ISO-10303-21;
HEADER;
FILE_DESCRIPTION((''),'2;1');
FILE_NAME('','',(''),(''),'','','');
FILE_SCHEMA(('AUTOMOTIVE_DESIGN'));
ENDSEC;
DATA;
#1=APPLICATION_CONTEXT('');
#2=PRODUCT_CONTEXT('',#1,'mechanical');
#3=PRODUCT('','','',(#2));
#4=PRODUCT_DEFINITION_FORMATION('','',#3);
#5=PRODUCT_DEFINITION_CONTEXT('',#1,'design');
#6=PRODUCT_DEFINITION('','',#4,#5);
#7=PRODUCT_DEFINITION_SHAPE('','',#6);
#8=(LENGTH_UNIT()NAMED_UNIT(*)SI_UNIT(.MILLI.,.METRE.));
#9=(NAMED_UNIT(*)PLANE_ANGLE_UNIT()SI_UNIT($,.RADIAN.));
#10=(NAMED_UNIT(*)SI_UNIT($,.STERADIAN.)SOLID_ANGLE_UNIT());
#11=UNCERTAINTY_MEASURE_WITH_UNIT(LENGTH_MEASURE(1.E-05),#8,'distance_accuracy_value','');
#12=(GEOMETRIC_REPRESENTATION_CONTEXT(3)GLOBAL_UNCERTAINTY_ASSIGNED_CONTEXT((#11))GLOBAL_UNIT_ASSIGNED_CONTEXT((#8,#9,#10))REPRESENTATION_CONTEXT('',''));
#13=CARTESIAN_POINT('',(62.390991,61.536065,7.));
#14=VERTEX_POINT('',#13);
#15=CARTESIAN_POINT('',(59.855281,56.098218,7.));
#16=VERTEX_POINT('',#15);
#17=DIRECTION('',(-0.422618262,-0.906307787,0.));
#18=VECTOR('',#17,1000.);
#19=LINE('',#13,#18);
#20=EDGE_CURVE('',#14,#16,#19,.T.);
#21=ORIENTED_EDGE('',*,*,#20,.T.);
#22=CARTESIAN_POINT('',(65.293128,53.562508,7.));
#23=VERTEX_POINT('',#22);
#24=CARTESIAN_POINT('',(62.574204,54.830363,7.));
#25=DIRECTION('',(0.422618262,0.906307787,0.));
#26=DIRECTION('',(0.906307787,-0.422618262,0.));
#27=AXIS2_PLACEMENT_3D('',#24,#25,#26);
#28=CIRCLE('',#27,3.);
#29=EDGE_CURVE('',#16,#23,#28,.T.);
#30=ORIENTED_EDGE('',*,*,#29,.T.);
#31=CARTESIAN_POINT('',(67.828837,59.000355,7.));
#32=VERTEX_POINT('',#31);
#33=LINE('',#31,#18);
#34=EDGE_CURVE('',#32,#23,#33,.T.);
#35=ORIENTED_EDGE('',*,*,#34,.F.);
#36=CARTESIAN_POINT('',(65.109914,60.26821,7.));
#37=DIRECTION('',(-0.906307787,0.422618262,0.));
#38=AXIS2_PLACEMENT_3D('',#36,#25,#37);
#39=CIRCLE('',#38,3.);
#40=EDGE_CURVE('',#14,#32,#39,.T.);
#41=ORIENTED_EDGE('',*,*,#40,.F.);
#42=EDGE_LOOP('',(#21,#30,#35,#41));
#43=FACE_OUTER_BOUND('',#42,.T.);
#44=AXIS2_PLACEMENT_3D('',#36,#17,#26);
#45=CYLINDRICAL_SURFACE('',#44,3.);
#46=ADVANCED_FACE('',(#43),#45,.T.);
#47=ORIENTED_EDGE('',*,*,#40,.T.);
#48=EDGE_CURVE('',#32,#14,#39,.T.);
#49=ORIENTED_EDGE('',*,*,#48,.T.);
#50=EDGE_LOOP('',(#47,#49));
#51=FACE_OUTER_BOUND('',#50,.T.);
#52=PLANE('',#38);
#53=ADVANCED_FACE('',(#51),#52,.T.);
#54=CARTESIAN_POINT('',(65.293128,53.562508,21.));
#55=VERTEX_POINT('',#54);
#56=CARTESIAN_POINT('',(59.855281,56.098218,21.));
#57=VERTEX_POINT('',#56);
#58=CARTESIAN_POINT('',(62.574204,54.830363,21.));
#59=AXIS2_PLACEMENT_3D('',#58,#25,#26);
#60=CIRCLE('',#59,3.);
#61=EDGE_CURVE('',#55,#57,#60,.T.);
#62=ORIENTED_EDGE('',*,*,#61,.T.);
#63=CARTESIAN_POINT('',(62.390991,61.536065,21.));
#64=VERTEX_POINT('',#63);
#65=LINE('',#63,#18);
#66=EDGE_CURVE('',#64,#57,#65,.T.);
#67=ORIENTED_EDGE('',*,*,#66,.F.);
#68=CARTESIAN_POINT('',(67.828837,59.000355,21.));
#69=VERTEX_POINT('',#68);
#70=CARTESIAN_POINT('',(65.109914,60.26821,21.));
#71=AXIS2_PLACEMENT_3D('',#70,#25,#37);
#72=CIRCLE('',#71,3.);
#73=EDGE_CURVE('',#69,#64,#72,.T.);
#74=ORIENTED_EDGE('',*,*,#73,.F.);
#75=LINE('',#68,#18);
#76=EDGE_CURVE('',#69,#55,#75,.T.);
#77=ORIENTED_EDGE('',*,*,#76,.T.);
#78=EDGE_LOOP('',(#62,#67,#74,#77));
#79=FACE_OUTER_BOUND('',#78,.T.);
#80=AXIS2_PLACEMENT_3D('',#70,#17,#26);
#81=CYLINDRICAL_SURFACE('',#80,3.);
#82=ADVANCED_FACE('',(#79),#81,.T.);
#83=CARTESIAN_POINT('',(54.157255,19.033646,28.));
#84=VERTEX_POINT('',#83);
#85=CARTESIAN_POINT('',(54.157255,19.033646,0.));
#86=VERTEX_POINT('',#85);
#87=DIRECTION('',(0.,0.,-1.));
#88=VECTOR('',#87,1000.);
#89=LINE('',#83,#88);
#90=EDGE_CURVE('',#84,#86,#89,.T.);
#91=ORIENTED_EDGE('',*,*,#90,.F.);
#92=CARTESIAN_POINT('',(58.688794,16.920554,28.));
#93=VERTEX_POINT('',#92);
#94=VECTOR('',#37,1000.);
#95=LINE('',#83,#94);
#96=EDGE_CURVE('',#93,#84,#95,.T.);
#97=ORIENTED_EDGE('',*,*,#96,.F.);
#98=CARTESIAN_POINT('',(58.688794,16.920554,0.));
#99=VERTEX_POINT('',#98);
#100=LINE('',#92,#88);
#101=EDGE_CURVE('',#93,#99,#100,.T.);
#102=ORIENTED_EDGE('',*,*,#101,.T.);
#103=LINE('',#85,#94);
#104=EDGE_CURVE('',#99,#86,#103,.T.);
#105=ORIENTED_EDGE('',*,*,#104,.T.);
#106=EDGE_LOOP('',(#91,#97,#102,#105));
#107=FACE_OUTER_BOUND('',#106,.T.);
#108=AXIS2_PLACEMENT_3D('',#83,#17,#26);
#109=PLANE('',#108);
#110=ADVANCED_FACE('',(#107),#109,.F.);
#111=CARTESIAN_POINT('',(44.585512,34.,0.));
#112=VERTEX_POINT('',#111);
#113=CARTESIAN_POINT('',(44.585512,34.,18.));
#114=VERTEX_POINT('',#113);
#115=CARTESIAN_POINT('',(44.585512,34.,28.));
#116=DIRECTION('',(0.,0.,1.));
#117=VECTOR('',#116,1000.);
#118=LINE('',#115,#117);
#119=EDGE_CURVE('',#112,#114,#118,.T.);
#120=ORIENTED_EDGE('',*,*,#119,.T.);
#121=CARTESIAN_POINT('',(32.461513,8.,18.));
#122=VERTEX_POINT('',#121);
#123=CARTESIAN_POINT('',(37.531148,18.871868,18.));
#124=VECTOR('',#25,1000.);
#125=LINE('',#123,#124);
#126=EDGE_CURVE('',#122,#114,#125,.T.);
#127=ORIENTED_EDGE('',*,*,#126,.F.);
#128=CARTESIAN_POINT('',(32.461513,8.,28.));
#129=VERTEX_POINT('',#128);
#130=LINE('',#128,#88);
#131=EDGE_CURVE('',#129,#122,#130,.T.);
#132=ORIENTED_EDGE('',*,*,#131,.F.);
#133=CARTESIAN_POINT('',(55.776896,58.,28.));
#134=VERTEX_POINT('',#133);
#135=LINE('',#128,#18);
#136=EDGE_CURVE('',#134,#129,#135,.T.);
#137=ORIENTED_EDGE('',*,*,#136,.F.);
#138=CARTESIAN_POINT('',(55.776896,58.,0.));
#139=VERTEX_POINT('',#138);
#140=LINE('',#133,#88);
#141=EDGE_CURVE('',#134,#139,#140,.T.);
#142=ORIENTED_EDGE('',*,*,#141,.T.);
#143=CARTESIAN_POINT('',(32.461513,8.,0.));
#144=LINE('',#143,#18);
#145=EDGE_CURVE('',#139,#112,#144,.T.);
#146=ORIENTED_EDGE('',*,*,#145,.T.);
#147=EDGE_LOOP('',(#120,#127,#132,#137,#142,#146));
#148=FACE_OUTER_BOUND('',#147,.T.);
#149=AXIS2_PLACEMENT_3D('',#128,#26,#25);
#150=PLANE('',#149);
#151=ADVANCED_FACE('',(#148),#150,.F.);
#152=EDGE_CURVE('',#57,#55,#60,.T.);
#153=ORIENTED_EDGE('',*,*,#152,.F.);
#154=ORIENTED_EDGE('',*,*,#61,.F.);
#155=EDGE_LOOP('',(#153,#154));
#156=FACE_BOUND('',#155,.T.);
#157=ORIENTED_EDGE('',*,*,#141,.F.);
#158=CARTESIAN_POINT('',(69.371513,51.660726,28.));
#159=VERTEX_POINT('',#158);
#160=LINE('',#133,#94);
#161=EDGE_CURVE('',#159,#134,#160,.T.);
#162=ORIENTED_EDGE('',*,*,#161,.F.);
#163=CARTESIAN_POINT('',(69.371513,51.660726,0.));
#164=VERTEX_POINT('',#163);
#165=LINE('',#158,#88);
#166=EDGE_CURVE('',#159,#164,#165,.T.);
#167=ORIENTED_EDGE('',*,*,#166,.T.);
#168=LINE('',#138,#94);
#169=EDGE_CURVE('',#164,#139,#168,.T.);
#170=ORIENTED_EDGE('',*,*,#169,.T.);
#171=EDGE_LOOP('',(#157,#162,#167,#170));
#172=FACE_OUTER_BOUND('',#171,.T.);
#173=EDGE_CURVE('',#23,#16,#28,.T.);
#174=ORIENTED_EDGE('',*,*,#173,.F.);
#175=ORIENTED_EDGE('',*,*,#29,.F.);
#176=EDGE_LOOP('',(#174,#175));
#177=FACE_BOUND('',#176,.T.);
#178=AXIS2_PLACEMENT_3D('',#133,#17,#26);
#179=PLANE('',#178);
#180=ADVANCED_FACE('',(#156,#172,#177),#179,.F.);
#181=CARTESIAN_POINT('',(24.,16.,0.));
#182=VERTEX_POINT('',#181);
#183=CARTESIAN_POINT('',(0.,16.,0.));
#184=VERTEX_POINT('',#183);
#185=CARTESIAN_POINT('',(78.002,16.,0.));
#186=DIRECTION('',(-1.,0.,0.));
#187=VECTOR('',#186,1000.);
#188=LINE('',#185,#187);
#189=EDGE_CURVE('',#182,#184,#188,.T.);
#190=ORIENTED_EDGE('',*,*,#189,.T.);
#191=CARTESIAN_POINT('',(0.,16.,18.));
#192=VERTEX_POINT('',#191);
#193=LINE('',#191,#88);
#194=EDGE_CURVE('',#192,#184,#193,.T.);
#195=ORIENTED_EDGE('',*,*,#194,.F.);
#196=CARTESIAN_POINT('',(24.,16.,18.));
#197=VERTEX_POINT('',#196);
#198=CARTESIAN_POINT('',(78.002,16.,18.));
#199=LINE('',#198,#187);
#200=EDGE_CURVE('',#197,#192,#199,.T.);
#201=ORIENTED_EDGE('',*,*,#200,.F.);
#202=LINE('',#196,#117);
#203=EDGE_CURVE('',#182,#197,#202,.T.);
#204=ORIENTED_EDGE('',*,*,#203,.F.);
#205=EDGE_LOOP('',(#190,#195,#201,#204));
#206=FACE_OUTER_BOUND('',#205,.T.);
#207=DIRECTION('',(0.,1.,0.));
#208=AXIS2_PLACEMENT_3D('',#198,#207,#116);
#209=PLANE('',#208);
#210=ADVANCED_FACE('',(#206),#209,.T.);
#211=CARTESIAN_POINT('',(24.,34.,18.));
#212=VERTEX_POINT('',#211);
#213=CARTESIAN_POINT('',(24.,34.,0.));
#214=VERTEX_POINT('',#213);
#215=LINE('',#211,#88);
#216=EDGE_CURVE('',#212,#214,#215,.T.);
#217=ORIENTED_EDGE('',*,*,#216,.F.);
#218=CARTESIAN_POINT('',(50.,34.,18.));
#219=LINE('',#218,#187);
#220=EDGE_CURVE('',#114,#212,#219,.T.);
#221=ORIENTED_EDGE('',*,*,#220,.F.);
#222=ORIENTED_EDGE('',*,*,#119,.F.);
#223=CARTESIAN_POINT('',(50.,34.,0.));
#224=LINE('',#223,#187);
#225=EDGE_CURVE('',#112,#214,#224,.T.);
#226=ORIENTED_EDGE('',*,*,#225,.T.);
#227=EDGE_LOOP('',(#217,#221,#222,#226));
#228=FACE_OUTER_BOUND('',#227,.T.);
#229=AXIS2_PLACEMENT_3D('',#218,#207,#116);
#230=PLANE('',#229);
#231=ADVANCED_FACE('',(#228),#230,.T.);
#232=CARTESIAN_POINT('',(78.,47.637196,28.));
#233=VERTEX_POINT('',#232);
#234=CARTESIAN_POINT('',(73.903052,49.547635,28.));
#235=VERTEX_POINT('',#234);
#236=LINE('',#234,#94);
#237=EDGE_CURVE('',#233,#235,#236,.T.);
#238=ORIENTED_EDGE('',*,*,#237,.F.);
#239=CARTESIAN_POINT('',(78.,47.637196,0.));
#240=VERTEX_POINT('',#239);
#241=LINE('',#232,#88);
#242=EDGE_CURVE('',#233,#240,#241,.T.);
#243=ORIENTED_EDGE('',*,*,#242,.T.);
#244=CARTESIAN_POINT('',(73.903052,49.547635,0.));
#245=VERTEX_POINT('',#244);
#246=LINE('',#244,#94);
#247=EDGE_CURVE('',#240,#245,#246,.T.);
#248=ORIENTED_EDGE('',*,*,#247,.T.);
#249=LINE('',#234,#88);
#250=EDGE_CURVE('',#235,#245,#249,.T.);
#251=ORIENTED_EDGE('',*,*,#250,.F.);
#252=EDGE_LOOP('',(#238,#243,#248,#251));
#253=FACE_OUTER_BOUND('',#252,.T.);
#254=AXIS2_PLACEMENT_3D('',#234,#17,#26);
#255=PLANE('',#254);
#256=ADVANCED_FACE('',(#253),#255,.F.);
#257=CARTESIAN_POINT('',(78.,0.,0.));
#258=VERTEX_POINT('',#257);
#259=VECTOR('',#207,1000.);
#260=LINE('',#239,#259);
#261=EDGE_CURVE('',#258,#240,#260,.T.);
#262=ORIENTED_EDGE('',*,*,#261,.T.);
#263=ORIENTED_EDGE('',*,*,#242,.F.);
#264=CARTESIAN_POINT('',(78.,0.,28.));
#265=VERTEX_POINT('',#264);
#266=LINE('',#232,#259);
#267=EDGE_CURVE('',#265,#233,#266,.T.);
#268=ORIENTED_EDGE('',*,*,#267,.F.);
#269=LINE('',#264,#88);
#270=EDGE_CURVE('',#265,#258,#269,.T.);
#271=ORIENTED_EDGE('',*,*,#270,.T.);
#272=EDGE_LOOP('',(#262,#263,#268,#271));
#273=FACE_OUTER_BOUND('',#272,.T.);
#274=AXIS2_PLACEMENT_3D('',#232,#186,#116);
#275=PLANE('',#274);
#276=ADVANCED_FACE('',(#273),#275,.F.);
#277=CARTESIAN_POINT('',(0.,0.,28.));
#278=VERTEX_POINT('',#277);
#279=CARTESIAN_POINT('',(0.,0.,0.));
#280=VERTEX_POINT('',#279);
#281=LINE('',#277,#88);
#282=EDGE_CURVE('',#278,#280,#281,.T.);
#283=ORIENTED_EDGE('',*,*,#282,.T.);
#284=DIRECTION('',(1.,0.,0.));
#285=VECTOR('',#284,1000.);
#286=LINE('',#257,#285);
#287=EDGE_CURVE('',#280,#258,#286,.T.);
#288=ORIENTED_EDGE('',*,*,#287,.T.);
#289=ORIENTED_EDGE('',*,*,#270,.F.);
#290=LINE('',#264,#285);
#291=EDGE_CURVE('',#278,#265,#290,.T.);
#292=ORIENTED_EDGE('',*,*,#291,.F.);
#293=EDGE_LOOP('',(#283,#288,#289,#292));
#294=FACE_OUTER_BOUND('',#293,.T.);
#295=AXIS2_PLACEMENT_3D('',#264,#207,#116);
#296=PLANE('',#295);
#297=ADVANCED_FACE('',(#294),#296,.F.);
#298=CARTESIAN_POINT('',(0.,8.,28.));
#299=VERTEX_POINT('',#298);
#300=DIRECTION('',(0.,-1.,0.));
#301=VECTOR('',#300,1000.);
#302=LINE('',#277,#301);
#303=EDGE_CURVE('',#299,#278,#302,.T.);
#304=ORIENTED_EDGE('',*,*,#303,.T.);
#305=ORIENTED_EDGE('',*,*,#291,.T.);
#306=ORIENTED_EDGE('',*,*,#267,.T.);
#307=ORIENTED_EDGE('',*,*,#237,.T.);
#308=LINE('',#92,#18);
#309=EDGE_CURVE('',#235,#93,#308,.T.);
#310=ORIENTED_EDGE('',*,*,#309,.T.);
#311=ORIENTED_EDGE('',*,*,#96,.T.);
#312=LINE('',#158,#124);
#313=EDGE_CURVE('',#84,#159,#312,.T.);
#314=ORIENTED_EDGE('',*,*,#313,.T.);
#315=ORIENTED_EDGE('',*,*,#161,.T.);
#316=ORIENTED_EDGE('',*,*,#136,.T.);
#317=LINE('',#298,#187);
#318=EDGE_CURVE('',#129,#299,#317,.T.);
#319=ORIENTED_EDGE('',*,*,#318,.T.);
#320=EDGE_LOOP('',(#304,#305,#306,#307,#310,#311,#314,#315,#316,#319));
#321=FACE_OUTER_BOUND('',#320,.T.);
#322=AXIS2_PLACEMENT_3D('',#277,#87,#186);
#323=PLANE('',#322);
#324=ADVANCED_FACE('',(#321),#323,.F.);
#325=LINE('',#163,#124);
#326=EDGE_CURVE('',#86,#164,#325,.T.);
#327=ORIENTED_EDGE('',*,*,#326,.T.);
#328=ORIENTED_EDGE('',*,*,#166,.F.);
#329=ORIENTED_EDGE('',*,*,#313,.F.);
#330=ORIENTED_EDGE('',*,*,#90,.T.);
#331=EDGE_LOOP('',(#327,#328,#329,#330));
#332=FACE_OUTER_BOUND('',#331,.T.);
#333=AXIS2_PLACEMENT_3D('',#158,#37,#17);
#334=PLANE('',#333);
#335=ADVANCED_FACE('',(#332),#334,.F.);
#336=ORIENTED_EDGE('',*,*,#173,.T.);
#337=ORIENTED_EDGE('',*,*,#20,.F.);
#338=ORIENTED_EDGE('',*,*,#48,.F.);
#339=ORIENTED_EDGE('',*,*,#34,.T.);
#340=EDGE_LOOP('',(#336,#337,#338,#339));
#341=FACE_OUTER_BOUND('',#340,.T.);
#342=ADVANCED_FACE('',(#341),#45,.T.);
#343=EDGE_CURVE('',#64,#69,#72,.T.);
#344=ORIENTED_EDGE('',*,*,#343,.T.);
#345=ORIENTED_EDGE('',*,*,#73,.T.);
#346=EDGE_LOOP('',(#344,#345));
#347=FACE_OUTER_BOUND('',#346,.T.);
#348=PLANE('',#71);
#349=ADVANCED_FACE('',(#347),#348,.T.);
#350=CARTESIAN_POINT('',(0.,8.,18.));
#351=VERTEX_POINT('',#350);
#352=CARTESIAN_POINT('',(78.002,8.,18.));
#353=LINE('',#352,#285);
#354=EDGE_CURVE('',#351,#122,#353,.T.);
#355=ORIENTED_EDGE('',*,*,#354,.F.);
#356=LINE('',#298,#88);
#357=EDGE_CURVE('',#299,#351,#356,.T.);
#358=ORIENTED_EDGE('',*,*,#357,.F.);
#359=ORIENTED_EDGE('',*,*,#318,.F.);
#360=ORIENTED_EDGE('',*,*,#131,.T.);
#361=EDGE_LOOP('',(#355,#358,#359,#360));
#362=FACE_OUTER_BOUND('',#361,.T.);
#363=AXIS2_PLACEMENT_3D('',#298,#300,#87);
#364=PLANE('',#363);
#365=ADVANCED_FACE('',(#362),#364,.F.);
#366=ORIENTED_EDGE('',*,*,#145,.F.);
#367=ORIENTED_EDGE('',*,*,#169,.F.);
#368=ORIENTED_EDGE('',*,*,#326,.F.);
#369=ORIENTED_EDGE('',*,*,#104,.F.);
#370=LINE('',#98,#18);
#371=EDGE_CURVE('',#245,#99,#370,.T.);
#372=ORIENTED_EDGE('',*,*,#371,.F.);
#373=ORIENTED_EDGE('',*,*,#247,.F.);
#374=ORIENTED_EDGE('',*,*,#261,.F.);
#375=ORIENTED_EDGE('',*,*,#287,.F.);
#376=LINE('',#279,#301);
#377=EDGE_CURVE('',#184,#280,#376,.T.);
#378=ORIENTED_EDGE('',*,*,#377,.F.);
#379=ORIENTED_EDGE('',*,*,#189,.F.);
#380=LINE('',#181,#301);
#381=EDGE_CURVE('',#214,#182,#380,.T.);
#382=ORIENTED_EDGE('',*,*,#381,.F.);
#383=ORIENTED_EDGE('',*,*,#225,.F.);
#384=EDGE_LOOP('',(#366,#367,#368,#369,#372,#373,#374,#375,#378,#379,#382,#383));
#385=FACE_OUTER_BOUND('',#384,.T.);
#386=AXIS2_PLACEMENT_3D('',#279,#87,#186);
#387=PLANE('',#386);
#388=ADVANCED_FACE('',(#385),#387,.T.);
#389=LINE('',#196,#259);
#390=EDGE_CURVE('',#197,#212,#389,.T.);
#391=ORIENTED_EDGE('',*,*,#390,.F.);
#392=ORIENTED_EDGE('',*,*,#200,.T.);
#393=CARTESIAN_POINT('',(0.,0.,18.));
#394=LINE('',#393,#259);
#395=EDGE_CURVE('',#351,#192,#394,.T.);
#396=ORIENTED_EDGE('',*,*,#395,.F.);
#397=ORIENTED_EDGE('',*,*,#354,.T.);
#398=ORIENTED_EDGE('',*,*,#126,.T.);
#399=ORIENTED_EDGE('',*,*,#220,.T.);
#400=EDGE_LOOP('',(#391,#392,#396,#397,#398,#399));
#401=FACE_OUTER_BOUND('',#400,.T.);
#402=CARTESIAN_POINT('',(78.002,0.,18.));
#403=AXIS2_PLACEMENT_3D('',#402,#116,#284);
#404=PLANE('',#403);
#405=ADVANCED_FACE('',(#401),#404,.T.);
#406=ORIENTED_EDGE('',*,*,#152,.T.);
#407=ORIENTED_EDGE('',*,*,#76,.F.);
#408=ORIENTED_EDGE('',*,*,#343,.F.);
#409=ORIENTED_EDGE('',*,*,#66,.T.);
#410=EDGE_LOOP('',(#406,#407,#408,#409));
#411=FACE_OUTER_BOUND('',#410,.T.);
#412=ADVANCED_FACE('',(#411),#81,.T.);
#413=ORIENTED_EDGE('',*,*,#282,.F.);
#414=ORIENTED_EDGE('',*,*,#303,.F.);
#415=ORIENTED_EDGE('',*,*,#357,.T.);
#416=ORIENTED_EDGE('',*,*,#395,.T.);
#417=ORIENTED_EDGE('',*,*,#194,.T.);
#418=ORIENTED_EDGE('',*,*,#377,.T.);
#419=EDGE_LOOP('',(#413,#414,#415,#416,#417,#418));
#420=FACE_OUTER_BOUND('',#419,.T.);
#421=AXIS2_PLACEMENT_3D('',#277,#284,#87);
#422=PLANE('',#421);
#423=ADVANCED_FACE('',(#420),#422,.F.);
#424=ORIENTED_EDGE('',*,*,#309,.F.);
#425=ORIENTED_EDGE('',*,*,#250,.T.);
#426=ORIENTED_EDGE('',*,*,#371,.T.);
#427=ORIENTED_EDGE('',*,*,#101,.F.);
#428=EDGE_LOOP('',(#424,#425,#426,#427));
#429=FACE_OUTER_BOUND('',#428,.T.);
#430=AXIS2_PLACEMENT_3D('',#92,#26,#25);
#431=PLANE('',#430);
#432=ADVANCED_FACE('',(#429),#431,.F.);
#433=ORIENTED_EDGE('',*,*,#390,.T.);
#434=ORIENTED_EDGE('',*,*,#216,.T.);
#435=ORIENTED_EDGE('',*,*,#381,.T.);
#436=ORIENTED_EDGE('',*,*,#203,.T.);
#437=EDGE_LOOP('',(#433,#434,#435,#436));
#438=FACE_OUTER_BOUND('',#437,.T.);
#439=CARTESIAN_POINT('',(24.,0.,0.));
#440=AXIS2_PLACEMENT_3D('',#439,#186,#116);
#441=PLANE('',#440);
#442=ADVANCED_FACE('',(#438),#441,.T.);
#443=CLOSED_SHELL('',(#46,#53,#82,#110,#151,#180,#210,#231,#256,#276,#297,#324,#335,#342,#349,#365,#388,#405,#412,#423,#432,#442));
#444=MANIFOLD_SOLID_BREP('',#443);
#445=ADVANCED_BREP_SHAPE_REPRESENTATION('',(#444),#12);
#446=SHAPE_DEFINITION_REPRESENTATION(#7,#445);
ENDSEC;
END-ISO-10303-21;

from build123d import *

# Parameters (mm, degrees)
STEPPED_BASE_BLOCK_DEPTH = 28
RISER_BLOCK_16X18_REACH  = 103.153
RISER_BLOCK_SKETCH_W     = 18
RISER_BLOCK_SKETCH_H     = 16
LOCATING_PINS_SKETCH_R   = 3
LOCATING_PINS_X2_DEPTH   = 6
ANGLED_HEAD_SKETCH_W     = 18
ANGLED_HEAD_SKETCH_H     = 18
ANGLED_HEAD_BLOCK_DEPTH  = 26


with BuildPart() as part:
    # Base Profile Sketch → Stepped Base Block (new body)
    with BuildSketch(Plane.XY):
        Polygon((0, 0), (0, 8), (32.461513138, 8), (55.776896046, 58), (69.371512852, 51.660726074), (54.157255429, 19.033645741), (58.688794364, 16.920554432), (73.903051787, 49.547634765), (78, 47.637196438), (78, 0), align=None)
    extrude(amount=STEPPED_BASE_BLOCK_DEPTH)

    # Riser Block 16x18: up to this plane
    riser_block_16x18_end = Plane(origin=(32.461513138, 8, 28), z_dir=(0.9063077870366479, -0.42261826174070377, 0))
    # Riser Block Sketch → Riser Block 16x18 (add, up to the surface)
    with BuildSketch(Plane.ZY, mode=Mode.PRIVATE) as riser_block_16x18_sk1:
        with Locations((9, 8)):
            Rectangle(RISER_BLOCK_SKETCH_W, RISER_BLOCK_SKETCH_H)
    riser_block_16x18_tool1 = split(extrude(riser_block_16x18_sk1.sketch, amount=-RISER_BLOCK_16X18_REACH, mode=Mode.PRIVATE), bisect_by=riser_block_16x18_end, keep=Keep.BOTH, mode=Mode.PRIVATE)
    add(riser_block_16x18_tool1.solids().sort_by_distance((0, 8, 9))[0])

    # Locating Pins Sketch → Locating Pins x2 (add)
    with BuildSketch(Plane(origin=(32.177388031, 69.004631316, 0), x_dir=(0.9063077870366478, -0.42261826174070405, 0), z_dir=(0.4226182617407041, 0.9063077870366479, 0))):
        with Locations((33.539176042, -7)):
            Circle(LOCATING_PINS_SKETCH_R)
        with Locations((33.539176042, -21)):
            Circle(LOCATING_PINS_SKETCH_R)
    extrude(amount=LOCATING_PINS_X2_DEPTH)

    # Angled Head Sketch → Angled Head Block (add)
    with BuildSketch(Plane.ZY.offset(-24)):
        with Locations((9, 25)):
            Rectangle(ANGLED_HEAD_SKETCH_W, ANGLED_HEAD_SKETCH_H)
    extrude(amount=-ANGLED_HEAD_BLOCK_DEPTH)


solid = part.part
